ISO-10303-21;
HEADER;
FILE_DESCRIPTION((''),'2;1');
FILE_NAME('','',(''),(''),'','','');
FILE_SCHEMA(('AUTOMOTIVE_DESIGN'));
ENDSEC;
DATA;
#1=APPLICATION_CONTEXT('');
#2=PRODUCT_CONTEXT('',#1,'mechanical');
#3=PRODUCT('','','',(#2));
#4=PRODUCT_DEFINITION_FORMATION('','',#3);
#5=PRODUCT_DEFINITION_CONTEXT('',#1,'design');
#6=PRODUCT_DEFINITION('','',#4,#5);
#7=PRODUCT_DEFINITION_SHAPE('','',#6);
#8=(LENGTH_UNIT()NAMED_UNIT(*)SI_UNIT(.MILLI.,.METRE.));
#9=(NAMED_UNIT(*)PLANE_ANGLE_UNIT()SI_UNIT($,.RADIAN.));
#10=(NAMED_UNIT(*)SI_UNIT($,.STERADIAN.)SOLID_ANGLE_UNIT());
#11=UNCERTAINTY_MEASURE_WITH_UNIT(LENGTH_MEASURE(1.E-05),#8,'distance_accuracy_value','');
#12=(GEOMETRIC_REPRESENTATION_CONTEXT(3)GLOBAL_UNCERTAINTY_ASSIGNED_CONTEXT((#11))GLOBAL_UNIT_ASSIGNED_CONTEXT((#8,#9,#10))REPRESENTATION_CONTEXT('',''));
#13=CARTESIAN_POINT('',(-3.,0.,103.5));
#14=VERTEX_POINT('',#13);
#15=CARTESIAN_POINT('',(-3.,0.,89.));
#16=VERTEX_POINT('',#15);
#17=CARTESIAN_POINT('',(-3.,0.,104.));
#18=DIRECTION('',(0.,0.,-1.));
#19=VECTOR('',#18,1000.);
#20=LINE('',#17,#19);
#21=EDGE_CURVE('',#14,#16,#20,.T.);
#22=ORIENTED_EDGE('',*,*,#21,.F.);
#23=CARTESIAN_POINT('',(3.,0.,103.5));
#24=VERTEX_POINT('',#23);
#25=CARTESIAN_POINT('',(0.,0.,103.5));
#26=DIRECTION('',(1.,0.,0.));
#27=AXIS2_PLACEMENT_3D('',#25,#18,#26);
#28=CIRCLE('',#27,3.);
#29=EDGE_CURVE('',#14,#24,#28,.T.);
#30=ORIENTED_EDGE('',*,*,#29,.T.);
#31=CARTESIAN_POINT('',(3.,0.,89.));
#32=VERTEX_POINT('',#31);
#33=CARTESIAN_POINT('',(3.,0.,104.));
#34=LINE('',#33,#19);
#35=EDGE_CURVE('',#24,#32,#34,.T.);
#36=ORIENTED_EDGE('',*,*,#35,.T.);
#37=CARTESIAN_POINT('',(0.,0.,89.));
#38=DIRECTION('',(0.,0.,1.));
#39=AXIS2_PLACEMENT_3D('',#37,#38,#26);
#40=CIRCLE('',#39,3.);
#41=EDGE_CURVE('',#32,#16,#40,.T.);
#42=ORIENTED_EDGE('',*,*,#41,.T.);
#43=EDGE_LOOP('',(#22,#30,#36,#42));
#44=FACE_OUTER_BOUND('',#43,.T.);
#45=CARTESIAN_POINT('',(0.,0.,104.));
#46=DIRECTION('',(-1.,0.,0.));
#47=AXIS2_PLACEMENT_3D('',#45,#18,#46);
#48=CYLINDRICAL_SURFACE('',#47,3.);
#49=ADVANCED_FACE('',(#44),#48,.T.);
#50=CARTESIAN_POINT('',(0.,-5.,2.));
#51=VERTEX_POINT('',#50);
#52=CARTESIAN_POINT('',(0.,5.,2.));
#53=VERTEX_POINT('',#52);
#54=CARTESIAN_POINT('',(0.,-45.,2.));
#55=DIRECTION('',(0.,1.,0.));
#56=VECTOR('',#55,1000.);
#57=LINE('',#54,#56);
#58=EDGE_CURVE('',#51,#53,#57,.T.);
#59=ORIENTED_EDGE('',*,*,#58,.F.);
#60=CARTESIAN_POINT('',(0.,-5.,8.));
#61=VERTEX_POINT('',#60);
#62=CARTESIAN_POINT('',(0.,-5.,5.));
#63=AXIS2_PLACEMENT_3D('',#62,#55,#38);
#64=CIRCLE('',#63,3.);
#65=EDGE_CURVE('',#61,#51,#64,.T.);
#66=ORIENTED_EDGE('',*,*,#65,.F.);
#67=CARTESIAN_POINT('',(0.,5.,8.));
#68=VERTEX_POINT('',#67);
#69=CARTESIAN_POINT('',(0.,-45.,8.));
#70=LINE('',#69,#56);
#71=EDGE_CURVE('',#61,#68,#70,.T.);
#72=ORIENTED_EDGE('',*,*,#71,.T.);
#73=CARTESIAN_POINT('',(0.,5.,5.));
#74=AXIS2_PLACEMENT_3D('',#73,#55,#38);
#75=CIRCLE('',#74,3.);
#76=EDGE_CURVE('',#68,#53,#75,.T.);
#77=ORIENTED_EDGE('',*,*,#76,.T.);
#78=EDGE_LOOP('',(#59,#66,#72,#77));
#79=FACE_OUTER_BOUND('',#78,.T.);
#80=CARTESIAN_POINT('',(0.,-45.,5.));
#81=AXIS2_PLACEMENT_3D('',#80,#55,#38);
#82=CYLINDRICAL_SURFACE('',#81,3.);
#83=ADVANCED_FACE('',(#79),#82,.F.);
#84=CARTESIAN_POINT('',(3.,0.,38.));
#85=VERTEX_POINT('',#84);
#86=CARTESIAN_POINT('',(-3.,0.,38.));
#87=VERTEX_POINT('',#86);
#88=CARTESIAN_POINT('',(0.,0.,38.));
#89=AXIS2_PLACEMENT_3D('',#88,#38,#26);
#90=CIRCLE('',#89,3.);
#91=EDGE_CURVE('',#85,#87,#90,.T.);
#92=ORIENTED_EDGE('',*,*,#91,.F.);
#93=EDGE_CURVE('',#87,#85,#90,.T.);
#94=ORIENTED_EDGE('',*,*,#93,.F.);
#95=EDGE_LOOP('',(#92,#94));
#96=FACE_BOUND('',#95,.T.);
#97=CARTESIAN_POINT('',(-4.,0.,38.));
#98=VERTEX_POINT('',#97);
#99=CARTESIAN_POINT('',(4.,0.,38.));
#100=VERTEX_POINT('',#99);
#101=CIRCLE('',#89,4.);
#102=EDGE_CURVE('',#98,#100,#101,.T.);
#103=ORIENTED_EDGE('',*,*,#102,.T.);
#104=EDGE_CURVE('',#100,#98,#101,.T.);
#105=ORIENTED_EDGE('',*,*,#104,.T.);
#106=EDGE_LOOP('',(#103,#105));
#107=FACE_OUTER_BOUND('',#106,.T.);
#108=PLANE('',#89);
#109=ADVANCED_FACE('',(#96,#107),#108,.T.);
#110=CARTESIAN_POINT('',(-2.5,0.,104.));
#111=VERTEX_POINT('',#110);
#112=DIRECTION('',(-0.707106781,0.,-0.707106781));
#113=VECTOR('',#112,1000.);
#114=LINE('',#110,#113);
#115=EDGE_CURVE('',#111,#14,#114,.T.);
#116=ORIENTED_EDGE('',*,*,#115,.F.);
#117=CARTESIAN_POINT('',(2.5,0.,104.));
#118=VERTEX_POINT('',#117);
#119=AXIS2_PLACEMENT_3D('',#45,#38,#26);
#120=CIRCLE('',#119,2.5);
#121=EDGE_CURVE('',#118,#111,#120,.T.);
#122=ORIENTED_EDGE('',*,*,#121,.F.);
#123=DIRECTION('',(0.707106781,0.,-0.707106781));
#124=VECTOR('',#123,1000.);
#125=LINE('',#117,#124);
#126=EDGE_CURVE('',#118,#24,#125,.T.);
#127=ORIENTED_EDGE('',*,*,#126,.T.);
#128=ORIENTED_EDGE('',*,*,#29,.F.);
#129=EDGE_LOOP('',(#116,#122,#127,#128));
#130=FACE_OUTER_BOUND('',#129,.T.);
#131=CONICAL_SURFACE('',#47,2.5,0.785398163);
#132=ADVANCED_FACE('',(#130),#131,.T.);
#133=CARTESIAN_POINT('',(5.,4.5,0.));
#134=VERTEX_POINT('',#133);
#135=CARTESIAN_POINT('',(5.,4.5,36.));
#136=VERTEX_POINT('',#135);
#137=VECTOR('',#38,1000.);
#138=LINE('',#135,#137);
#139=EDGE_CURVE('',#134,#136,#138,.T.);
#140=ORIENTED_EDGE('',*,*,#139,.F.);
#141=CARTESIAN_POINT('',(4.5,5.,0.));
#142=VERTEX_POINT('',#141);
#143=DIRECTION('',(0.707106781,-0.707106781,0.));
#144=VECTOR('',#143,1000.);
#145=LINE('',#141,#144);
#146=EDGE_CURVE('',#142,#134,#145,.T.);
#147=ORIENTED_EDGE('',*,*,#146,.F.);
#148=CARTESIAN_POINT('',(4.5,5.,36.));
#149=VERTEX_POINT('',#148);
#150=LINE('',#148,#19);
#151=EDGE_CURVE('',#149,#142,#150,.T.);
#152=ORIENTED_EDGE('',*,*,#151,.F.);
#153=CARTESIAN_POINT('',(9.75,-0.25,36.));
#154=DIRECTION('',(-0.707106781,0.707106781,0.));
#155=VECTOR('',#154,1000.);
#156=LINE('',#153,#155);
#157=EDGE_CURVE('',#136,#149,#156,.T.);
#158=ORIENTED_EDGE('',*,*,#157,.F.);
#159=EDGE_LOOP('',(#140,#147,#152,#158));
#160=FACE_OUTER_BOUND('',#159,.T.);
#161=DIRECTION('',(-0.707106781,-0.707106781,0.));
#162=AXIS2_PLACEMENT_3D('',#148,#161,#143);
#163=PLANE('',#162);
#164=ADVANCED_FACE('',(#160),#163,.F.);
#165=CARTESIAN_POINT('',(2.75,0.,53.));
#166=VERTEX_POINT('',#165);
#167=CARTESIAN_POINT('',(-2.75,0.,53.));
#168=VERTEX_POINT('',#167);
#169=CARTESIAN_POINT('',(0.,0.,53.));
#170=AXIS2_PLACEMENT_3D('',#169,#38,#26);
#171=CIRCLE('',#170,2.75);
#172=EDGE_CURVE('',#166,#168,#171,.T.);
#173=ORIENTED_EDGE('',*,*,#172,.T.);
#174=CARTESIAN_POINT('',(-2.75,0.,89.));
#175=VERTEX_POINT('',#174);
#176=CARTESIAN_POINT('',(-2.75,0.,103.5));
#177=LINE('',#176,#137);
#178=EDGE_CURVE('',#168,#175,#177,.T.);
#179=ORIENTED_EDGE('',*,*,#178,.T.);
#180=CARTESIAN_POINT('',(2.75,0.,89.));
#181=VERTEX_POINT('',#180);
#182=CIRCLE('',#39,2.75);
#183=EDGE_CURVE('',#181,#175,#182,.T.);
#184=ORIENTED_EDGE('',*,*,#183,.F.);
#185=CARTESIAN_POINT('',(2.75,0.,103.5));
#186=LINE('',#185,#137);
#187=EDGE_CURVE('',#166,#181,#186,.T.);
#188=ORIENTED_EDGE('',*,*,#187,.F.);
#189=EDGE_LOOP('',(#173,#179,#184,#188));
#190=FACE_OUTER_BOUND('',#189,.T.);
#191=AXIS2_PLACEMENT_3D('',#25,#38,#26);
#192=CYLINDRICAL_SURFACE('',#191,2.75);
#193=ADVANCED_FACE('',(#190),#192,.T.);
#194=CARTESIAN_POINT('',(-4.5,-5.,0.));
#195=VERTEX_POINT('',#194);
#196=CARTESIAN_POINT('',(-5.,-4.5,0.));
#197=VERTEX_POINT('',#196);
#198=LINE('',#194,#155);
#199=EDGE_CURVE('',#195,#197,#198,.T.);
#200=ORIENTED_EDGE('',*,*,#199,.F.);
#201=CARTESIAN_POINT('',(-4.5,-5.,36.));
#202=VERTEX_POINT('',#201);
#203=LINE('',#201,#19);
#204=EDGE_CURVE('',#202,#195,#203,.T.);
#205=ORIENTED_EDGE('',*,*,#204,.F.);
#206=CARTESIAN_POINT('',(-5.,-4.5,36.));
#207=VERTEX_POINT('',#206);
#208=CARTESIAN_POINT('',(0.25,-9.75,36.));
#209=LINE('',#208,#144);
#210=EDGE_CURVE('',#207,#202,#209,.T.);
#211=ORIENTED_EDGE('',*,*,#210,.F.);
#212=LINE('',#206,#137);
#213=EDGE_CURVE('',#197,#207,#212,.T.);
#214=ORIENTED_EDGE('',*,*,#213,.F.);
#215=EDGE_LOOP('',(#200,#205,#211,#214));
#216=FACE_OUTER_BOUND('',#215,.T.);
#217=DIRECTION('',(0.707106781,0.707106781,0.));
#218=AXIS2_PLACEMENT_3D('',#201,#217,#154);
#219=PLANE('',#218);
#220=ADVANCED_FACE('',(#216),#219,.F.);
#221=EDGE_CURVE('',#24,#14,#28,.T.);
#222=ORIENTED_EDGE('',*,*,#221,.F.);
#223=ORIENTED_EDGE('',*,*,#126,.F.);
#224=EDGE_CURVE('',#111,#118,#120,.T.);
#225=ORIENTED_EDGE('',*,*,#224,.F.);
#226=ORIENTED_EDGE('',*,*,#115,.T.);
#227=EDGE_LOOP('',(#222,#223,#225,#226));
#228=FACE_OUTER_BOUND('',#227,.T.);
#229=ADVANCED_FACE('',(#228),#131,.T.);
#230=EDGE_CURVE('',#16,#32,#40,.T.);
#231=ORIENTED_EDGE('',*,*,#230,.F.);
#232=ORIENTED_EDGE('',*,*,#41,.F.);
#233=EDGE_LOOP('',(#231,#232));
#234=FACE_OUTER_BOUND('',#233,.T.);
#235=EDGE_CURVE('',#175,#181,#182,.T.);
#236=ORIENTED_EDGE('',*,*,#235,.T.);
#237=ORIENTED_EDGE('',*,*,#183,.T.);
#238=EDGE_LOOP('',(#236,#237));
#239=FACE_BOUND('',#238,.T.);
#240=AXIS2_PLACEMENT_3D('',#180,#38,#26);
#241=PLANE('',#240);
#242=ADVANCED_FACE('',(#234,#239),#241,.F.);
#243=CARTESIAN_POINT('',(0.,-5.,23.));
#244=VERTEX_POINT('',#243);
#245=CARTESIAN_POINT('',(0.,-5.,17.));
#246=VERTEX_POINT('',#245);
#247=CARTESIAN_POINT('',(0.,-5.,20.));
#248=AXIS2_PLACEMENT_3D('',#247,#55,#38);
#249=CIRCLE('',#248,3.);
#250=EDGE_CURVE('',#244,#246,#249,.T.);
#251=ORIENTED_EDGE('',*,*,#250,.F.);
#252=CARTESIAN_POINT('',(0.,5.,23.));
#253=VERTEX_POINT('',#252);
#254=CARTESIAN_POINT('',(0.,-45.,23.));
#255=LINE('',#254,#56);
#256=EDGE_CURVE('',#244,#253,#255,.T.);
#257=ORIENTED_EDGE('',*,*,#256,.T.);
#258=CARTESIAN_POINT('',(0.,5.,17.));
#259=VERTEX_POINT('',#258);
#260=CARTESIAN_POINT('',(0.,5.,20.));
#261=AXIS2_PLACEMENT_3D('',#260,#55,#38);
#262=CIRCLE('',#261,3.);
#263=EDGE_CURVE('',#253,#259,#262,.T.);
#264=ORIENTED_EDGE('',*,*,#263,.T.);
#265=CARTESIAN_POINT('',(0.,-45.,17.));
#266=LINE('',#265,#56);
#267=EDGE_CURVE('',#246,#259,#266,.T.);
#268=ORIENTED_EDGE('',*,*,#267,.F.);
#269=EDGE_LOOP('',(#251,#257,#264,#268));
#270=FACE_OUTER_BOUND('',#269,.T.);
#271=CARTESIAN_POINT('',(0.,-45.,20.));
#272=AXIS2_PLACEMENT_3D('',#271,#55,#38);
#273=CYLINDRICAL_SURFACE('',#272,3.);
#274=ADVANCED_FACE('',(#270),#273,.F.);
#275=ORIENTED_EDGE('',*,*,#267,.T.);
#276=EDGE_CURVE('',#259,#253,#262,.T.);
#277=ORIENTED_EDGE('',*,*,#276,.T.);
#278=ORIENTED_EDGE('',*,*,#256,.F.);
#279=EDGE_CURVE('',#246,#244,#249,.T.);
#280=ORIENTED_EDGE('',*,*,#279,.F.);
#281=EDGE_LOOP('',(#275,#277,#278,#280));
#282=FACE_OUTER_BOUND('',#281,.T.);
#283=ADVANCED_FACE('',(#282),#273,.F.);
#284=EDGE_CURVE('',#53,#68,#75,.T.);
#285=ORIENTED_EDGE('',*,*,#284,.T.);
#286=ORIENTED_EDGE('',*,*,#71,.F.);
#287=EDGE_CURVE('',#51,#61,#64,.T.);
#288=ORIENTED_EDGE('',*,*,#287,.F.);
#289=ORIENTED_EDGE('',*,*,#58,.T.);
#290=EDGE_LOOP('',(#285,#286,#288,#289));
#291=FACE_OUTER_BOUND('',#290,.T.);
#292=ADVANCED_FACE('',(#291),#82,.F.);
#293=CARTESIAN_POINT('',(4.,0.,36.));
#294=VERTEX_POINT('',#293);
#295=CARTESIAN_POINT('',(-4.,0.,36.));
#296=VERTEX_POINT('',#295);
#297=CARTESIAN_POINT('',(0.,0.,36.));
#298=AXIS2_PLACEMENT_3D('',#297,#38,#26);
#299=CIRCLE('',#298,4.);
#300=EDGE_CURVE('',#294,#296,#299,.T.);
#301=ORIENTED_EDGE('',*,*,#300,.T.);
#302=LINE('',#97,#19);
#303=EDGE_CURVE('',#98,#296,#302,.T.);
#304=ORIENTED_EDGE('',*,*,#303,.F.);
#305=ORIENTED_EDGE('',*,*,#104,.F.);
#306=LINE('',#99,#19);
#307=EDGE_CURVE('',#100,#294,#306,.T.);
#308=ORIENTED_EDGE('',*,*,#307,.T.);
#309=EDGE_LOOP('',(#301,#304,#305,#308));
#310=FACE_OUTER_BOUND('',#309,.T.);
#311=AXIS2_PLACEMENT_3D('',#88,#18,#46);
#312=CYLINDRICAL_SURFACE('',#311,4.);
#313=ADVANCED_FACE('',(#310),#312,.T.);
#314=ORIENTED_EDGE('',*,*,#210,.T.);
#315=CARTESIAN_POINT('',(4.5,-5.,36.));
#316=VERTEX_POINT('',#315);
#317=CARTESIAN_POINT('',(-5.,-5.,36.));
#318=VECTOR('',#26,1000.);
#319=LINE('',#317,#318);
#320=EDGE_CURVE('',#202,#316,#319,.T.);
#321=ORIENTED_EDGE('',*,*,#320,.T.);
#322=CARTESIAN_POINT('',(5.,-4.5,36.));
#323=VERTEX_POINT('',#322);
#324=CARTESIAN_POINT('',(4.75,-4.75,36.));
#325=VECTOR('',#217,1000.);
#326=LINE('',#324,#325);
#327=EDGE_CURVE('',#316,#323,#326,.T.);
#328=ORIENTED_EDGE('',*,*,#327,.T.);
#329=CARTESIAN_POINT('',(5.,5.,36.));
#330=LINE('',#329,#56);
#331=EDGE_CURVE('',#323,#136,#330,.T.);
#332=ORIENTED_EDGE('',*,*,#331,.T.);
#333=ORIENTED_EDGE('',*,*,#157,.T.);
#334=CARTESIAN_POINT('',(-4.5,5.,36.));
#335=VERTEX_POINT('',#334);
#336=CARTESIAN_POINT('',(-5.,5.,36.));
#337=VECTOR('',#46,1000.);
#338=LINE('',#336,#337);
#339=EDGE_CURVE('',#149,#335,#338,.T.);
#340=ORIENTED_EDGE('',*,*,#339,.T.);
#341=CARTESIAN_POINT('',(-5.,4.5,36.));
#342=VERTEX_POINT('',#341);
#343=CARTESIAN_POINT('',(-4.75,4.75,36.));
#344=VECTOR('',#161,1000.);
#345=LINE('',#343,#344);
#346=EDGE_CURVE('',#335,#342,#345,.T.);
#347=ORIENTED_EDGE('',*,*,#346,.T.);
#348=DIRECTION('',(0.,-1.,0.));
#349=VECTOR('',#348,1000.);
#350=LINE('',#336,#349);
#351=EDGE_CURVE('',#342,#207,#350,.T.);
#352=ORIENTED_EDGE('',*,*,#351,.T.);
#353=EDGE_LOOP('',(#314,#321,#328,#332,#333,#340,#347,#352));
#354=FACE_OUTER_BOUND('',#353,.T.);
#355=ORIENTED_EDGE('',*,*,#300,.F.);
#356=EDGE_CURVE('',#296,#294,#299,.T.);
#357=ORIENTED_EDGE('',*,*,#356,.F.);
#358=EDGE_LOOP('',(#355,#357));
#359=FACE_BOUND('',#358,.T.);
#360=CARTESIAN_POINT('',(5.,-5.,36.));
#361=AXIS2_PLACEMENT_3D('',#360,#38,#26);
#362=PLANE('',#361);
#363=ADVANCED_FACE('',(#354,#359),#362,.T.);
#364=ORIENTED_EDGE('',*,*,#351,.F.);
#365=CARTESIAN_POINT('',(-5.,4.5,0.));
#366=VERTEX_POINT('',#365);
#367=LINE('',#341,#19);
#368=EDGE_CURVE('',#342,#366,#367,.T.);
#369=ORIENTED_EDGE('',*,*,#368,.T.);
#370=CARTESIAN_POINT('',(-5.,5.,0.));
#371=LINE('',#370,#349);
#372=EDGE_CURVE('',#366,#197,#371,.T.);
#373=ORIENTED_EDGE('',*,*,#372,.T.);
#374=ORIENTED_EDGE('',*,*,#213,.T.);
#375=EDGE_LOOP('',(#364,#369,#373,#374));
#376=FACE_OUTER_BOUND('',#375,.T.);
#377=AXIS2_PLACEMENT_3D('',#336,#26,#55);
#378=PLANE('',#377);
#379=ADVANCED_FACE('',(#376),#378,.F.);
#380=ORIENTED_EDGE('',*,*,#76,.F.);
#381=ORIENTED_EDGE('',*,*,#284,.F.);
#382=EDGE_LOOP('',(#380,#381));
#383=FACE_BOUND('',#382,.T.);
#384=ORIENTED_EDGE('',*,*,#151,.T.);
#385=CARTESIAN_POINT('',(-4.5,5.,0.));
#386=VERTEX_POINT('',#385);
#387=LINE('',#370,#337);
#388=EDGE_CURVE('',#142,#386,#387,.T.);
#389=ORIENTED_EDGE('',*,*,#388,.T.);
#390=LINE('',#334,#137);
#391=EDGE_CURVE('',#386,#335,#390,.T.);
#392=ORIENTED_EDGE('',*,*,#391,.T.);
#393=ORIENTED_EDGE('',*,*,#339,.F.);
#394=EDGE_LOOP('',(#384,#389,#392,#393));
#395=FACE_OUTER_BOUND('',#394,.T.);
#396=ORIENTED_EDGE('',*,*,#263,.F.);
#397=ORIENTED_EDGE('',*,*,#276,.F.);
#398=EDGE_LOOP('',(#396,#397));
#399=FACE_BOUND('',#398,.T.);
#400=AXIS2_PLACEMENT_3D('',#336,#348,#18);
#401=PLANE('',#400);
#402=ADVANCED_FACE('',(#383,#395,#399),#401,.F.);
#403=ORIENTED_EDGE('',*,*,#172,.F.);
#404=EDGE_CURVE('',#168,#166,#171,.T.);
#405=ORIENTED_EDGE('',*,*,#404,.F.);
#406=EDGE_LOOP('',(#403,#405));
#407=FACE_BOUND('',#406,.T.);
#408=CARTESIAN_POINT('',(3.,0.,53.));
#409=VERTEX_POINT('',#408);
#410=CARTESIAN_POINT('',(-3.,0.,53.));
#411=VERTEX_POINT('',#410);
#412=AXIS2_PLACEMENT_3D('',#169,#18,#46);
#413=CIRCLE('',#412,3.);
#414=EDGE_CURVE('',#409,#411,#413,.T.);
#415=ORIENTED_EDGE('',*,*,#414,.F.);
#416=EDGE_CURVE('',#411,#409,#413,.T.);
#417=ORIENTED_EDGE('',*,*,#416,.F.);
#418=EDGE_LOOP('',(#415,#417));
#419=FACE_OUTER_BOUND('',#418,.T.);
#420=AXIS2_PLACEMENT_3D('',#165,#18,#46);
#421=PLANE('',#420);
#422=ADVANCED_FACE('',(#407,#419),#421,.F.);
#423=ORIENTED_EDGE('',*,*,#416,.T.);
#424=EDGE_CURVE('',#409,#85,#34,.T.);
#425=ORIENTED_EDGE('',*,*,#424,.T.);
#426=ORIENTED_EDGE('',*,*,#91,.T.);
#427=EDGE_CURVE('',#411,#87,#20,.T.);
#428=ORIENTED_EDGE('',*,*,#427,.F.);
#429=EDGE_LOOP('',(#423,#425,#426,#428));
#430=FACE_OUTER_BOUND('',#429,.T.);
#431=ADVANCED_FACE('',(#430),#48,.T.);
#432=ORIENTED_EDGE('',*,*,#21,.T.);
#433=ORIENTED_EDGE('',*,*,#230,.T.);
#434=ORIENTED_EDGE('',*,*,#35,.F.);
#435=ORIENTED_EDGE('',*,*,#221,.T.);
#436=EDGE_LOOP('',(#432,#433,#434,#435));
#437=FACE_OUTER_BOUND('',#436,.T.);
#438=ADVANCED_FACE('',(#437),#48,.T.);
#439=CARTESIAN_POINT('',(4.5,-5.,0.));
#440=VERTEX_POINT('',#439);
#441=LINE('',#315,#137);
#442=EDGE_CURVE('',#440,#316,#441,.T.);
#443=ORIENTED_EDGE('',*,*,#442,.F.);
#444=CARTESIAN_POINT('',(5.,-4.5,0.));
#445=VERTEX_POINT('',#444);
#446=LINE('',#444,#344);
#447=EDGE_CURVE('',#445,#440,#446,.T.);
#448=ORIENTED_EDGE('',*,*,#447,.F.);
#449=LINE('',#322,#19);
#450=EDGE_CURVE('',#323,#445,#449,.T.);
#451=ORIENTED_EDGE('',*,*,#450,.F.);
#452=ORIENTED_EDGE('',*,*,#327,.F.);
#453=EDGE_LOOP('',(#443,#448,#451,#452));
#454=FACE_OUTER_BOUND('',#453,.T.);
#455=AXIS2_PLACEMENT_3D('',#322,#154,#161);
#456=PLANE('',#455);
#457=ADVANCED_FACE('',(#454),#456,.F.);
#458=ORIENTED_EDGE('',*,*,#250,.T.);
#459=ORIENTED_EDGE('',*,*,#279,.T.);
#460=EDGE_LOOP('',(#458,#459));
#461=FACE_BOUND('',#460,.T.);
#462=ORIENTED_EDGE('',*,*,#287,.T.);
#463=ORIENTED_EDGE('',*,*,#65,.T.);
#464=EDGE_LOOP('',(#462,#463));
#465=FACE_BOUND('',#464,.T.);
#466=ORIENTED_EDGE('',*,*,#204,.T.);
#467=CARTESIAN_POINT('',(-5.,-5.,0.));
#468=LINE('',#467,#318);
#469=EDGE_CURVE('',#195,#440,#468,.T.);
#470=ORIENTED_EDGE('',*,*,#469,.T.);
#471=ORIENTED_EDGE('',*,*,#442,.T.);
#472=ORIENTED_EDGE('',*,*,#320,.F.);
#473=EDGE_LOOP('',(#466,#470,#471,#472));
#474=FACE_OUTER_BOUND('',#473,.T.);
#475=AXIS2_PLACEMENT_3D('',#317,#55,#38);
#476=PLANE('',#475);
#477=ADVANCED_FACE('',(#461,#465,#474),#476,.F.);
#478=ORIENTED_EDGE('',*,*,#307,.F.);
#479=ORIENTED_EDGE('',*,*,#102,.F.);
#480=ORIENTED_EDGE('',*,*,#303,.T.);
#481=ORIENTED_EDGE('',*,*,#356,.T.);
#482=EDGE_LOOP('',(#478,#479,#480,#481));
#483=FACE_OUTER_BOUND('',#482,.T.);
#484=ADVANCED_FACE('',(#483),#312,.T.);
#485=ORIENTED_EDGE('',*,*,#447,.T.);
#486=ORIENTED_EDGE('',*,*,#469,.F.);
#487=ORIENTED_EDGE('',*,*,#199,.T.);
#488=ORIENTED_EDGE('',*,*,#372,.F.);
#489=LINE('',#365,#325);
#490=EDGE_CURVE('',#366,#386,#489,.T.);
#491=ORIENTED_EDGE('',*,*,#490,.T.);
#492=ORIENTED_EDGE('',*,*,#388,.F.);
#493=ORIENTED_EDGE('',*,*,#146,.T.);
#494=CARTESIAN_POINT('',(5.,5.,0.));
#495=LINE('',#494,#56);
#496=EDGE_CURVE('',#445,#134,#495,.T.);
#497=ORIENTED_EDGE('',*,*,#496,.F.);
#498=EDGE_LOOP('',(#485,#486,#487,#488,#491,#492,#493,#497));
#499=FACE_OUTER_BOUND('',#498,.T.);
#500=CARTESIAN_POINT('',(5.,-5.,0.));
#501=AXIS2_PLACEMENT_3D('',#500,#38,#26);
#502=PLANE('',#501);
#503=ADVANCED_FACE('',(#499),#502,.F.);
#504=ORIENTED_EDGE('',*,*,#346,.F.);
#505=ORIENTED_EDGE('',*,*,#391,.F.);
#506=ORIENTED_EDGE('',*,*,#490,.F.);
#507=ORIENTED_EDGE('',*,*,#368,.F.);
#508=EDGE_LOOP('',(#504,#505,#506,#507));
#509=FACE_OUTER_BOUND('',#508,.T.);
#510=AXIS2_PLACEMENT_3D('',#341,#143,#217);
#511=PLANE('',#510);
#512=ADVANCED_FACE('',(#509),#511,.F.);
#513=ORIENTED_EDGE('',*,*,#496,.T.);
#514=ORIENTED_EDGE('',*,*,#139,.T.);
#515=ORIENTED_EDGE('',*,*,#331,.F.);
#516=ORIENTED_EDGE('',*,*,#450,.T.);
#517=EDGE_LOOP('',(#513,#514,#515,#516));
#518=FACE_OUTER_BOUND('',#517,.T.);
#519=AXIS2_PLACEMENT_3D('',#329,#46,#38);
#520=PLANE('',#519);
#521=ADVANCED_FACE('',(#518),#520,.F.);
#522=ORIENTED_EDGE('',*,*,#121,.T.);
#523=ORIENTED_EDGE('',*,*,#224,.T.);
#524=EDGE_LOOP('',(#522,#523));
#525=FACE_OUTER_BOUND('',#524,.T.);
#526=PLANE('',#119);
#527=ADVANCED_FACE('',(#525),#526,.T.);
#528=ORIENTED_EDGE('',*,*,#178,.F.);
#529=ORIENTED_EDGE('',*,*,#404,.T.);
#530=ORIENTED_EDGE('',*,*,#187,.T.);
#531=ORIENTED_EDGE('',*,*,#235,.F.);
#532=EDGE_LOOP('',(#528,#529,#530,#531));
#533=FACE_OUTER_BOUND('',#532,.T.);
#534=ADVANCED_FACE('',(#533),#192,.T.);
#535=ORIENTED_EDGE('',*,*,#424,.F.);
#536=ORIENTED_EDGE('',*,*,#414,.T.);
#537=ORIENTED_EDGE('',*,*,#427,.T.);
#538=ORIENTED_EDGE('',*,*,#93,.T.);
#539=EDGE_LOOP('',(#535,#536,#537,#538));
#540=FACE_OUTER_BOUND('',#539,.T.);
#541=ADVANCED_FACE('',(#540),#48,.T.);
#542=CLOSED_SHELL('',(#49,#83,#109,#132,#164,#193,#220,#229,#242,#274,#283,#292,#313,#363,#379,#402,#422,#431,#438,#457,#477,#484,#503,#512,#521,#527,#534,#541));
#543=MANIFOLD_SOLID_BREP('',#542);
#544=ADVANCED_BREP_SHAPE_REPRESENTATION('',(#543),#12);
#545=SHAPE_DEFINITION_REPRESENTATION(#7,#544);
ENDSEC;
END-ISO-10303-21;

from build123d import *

# Parameters (mm, degrees)
SKETCH1_W           = 10
SKETCH1_H           = 10
BOSS_EXTRUDE1_DEPTH = 36
SKETCH2_R           = 4
BOSS_EXTRUDE2_DEPTH = 2
SKETCH3_R           = 3
BOSS_EXTRUDE3_DEPTH = 66
SKETCH4_R           = 3
CUT_EXTRUDE1_DEPTH  = 50
CHAMFER1_SIZE       = 0.5
CHAMFER2_SIZE       = 0.5
SKETCH6_W           = 5
SKETCH6_H           = 36


with BuildPart() as part:
    # Sketch1 → Boss-Extrude1 (new body)
    with BuildSketch(Plane.XY):
        Rectangle(SKETCH1_W, SKETCH1_H)
    extrude(amount=BOSS_EXTRUDE1_DEPTH)

    # Sketch2 → Boss-Extrude2 (add)
    with BuildSketch(Plane.XY.offset(36)):
        Circle(SKETCH2_R)
    extrude(amount=BOSS_EXTRUDE2_DEPTH)

    # Sketch3 → Boss-Extrude3 (add)
    with BuildSketch(Plane.XY.offset(38)):
        Circle(SKETCH3_R)
    extrude(amount=BOSS_EXTRUDE3_DEPTH)

    # Sketch4 → Cut-Extrude1 (cut)
    with BuildSketch(Plane(origin=(0, 5, 0), x_dir=(1, 0, 0), z_dir=(0, 1, 0))):
        with Locations(Location((0, -5, 0), (0, 0, 270))):
            Circle(SKETCH4_R)
        with Locations(Location((0, -20, 0), (0, 0, 270))):
            Circle(SKETCH4_R)
    extrude(amount=-CUT_EXTRUDE1_DEPTH, mode=Mode.SUBTRACT)

    # Chamfer1
    chamfer1_edges = [part.edges().sort_by_distance(p)[0] for p in [
        (5, -5, 18),
        (-5, -5, 18),
        (-5, 5, 18),
        (5, 5, 18),
    ]]
    chamfer(chamfer1_edges, length=CHAMFER1_SIZE)

    # Chamfer2
    chamfer2_edges = [part.edges().sort_by_distance(p)[0] for p in [
        (-3, 0, 104),
    ]]
    chamfer(chamfer2_edges, length=CHAMFER2_SIZE)

    # Sketch6 → Cut-Revolve1 (revolve, cut)
    with BuildSketch(Plane(origin=(0, 0, 0), x_dir=(1, 0, 0), z_dir=(0, 1, 0))):
        with Locations((5.25, -71)):
            Rectangle(SKETCH6_W, SKETCH6_H)
    revolve(axis=Axis((0, 0, 103.5), (0, 0, -1)), mode=Mode.SUBTRACT)


solid = part.part
